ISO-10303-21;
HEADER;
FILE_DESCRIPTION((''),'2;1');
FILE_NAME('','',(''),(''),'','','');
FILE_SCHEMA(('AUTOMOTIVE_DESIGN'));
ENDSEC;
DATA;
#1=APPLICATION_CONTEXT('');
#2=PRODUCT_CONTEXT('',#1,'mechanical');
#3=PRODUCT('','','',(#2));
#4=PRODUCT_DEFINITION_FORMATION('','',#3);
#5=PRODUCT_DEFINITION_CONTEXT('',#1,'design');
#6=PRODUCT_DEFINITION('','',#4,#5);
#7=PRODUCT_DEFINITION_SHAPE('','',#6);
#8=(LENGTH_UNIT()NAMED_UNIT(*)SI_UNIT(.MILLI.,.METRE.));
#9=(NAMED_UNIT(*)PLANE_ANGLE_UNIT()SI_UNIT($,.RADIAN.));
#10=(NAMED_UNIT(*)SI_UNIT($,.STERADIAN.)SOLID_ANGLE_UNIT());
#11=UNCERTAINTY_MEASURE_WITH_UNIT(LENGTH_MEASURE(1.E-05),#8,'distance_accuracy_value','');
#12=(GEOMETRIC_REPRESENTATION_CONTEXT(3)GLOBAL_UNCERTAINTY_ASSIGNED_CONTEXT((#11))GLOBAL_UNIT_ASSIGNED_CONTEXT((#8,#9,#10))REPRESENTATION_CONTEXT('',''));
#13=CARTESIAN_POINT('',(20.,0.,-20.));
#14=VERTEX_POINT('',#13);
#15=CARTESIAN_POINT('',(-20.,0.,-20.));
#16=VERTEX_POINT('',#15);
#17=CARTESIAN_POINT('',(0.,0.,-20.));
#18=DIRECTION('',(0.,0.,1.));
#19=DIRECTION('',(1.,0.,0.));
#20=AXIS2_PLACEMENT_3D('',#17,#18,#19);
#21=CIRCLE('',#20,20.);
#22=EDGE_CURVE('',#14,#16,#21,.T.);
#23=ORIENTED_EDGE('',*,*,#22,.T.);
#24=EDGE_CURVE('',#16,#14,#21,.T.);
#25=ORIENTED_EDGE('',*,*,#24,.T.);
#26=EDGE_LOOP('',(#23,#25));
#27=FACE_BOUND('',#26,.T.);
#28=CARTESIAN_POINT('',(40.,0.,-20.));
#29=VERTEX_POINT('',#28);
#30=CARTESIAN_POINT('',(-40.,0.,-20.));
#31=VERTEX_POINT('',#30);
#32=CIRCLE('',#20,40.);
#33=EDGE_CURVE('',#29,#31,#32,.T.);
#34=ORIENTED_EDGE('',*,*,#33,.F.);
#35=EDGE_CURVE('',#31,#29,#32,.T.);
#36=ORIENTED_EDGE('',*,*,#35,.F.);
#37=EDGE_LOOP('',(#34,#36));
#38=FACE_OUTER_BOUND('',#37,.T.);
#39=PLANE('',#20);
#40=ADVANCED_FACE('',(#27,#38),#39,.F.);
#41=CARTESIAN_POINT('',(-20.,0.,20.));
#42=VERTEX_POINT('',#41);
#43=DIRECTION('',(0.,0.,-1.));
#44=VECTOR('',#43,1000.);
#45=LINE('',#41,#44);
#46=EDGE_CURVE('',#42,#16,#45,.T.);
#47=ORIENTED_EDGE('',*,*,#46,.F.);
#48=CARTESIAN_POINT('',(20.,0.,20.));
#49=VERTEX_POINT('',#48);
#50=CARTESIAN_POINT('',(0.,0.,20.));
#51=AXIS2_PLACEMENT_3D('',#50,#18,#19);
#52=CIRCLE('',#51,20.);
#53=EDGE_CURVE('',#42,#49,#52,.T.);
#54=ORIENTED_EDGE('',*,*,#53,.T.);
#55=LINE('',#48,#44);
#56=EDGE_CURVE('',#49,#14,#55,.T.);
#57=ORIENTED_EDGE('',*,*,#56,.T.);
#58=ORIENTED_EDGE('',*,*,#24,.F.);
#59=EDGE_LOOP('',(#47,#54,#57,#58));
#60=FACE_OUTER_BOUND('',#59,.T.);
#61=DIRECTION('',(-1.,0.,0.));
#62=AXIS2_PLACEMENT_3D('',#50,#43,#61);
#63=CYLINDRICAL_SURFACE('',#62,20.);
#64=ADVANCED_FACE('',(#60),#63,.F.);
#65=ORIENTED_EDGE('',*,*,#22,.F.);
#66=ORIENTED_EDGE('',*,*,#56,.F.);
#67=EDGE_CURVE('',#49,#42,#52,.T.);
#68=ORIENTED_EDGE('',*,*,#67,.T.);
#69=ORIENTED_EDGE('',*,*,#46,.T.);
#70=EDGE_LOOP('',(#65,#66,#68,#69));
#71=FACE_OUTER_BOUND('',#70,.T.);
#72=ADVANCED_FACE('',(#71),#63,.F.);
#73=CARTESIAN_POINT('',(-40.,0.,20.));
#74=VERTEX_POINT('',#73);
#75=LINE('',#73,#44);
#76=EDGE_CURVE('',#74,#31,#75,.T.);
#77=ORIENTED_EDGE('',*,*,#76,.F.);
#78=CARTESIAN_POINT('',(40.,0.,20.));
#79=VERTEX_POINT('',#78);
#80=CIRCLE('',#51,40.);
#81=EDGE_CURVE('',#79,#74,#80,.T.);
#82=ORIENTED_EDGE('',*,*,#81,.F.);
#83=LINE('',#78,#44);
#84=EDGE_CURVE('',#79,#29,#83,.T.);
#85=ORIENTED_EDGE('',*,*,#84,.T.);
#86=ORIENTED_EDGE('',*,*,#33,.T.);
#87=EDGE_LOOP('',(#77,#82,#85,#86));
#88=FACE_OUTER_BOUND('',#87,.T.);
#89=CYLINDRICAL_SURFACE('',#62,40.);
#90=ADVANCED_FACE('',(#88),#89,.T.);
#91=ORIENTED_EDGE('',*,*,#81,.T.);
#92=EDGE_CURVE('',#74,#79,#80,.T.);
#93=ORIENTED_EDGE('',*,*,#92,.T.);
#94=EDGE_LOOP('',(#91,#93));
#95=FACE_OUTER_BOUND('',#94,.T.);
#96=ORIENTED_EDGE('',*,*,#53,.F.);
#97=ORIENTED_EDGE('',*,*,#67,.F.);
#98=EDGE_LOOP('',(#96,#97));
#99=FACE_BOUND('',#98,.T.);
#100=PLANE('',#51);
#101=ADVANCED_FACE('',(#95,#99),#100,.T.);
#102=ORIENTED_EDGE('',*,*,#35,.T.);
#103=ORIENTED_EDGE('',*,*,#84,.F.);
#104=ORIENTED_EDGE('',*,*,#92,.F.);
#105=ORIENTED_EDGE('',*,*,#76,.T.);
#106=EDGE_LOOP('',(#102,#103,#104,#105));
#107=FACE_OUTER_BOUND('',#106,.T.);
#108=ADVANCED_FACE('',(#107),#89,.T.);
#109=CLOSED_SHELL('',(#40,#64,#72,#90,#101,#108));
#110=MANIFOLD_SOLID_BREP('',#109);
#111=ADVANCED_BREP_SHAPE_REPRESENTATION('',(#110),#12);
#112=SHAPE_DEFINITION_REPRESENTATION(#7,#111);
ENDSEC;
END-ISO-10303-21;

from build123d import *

# Parameters (mm, degrees)
SKETCH_1_R      = 40
SKETCH_1_R_2    = 20
EXTRUDE_1_DEPTH = 20


with BuildPart() as part:
    # 草图1 → 凸台-拉伸1 (new, symmetric)
    with BuildSketch(Plane.XY):
        Circle(SKETCH_1_R)
        Circle(SKETCH_1_R_2, mode=Mode.SUBTRACT)
    extrude(amount=EXTRUDE_1_DEPTH, both=True)


solid = part.part
